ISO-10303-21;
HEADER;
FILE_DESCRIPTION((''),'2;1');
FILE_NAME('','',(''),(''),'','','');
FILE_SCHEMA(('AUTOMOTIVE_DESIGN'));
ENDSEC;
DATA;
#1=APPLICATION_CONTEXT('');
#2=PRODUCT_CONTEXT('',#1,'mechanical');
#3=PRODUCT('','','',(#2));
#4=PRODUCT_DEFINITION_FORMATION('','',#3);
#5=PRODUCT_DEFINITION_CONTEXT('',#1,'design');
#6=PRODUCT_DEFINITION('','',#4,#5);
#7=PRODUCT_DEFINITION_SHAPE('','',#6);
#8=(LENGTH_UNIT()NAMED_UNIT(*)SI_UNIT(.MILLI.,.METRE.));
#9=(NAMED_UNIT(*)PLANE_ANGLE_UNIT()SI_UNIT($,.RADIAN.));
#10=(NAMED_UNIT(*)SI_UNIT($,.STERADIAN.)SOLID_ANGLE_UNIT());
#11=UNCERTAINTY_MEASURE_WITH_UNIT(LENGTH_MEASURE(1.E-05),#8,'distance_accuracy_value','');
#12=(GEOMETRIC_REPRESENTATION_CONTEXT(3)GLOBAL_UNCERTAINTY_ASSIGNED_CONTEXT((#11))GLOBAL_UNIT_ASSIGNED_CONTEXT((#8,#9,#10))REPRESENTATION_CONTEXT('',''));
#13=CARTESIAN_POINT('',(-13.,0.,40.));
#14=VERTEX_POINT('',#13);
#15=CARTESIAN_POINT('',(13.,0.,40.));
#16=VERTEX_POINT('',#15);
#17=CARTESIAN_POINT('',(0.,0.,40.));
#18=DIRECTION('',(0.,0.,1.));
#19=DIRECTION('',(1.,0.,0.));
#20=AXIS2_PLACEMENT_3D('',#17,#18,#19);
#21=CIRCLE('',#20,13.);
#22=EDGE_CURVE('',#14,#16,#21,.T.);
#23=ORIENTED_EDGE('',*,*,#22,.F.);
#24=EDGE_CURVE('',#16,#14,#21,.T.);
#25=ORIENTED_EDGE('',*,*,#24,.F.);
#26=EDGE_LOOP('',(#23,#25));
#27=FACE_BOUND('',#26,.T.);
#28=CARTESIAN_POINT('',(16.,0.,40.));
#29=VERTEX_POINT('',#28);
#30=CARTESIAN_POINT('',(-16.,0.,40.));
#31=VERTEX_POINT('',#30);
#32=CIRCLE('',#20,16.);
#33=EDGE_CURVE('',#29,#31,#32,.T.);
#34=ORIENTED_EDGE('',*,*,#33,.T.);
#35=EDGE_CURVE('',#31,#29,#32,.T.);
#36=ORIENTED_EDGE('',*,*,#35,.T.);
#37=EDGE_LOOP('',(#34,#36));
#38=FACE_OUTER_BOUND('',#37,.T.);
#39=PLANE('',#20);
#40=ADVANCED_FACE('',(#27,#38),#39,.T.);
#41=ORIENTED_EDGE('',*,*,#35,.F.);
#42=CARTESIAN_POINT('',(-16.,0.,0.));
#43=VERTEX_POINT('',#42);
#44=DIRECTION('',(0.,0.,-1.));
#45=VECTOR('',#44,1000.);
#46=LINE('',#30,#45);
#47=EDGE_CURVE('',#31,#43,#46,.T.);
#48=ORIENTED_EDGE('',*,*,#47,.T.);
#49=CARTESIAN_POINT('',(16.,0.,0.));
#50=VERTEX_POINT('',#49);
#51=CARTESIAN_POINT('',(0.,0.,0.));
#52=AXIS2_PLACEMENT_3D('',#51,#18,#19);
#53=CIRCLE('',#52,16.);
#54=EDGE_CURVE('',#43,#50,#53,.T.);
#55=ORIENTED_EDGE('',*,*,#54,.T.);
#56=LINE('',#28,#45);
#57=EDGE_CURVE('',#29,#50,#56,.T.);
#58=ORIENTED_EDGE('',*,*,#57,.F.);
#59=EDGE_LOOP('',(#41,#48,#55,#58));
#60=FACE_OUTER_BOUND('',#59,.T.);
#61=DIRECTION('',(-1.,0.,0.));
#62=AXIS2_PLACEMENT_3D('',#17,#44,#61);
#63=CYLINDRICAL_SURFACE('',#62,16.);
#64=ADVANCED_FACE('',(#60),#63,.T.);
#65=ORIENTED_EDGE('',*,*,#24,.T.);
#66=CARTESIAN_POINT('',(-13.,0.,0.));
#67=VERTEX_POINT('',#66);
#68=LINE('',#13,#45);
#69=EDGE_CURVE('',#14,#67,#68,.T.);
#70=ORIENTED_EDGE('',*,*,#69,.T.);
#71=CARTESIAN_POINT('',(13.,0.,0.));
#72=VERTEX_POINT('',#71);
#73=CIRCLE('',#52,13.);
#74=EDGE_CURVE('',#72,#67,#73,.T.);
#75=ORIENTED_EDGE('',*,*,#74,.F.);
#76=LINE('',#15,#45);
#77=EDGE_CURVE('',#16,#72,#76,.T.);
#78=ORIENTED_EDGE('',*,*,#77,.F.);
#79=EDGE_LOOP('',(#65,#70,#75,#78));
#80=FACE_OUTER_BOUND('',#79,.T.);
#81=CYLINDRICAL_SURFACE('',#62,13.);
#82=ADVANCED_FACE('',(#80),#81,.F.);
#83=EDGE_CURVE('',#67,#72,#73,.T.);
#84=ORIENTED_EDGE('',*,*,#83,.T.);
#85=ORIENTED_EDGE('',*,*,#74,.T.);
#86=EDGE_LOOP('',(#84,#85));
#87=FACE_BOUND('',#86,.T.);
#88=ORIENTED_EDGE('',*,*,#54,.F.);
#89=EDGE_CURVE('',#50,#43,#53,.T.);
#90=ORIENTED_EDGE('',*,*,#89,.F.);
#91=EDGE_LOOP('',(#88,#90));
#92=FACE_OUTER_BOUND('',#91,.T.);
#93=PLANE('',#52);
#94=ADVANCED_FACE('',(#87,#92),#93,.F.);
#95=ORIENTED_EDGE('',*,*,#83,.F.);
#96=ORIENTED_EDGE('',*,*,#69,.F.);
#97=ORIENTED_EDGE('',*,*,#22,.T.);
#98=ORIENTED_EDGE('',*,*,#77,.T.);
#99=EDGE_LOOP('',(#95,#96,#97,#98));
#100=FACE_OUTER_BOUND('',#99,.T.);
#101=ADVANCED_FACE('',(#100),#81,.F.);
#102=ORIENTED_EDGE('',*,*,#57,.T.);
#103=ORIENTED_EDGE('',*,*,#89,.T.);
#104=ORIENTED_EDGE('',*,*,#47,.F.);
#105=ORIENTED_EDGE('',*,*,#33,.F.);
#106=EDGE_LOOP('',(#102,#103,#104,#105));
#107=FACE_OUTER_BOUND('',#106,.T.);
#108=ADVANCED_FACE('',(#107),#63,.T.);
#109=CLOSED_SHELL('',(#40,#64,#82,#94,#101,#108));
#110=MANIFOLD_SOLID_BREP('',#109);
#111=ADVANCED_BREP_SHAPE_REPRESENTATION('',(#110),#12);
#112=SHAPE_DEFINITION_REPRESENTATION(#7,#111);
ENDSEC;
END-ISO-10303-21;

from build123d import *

# Parameters (mm, degrees)
SKETCH_1_R      = 16
SKETCH_1_R_2    = 13
EXTRUDE_1_DEPTH = 40


with BuildPart() as part:
    # 草图1 → 拉伸-薄壁1 (new body)
    with BuildSketch(Plane.XY):
        Circle(SKETCH_1_R)
        Circle(SKETCH_1_R_2, mode=Mode.SUBTRACT)
    extrude(amount=EXTRUDE_1_DEPTH)


solid = part.part
